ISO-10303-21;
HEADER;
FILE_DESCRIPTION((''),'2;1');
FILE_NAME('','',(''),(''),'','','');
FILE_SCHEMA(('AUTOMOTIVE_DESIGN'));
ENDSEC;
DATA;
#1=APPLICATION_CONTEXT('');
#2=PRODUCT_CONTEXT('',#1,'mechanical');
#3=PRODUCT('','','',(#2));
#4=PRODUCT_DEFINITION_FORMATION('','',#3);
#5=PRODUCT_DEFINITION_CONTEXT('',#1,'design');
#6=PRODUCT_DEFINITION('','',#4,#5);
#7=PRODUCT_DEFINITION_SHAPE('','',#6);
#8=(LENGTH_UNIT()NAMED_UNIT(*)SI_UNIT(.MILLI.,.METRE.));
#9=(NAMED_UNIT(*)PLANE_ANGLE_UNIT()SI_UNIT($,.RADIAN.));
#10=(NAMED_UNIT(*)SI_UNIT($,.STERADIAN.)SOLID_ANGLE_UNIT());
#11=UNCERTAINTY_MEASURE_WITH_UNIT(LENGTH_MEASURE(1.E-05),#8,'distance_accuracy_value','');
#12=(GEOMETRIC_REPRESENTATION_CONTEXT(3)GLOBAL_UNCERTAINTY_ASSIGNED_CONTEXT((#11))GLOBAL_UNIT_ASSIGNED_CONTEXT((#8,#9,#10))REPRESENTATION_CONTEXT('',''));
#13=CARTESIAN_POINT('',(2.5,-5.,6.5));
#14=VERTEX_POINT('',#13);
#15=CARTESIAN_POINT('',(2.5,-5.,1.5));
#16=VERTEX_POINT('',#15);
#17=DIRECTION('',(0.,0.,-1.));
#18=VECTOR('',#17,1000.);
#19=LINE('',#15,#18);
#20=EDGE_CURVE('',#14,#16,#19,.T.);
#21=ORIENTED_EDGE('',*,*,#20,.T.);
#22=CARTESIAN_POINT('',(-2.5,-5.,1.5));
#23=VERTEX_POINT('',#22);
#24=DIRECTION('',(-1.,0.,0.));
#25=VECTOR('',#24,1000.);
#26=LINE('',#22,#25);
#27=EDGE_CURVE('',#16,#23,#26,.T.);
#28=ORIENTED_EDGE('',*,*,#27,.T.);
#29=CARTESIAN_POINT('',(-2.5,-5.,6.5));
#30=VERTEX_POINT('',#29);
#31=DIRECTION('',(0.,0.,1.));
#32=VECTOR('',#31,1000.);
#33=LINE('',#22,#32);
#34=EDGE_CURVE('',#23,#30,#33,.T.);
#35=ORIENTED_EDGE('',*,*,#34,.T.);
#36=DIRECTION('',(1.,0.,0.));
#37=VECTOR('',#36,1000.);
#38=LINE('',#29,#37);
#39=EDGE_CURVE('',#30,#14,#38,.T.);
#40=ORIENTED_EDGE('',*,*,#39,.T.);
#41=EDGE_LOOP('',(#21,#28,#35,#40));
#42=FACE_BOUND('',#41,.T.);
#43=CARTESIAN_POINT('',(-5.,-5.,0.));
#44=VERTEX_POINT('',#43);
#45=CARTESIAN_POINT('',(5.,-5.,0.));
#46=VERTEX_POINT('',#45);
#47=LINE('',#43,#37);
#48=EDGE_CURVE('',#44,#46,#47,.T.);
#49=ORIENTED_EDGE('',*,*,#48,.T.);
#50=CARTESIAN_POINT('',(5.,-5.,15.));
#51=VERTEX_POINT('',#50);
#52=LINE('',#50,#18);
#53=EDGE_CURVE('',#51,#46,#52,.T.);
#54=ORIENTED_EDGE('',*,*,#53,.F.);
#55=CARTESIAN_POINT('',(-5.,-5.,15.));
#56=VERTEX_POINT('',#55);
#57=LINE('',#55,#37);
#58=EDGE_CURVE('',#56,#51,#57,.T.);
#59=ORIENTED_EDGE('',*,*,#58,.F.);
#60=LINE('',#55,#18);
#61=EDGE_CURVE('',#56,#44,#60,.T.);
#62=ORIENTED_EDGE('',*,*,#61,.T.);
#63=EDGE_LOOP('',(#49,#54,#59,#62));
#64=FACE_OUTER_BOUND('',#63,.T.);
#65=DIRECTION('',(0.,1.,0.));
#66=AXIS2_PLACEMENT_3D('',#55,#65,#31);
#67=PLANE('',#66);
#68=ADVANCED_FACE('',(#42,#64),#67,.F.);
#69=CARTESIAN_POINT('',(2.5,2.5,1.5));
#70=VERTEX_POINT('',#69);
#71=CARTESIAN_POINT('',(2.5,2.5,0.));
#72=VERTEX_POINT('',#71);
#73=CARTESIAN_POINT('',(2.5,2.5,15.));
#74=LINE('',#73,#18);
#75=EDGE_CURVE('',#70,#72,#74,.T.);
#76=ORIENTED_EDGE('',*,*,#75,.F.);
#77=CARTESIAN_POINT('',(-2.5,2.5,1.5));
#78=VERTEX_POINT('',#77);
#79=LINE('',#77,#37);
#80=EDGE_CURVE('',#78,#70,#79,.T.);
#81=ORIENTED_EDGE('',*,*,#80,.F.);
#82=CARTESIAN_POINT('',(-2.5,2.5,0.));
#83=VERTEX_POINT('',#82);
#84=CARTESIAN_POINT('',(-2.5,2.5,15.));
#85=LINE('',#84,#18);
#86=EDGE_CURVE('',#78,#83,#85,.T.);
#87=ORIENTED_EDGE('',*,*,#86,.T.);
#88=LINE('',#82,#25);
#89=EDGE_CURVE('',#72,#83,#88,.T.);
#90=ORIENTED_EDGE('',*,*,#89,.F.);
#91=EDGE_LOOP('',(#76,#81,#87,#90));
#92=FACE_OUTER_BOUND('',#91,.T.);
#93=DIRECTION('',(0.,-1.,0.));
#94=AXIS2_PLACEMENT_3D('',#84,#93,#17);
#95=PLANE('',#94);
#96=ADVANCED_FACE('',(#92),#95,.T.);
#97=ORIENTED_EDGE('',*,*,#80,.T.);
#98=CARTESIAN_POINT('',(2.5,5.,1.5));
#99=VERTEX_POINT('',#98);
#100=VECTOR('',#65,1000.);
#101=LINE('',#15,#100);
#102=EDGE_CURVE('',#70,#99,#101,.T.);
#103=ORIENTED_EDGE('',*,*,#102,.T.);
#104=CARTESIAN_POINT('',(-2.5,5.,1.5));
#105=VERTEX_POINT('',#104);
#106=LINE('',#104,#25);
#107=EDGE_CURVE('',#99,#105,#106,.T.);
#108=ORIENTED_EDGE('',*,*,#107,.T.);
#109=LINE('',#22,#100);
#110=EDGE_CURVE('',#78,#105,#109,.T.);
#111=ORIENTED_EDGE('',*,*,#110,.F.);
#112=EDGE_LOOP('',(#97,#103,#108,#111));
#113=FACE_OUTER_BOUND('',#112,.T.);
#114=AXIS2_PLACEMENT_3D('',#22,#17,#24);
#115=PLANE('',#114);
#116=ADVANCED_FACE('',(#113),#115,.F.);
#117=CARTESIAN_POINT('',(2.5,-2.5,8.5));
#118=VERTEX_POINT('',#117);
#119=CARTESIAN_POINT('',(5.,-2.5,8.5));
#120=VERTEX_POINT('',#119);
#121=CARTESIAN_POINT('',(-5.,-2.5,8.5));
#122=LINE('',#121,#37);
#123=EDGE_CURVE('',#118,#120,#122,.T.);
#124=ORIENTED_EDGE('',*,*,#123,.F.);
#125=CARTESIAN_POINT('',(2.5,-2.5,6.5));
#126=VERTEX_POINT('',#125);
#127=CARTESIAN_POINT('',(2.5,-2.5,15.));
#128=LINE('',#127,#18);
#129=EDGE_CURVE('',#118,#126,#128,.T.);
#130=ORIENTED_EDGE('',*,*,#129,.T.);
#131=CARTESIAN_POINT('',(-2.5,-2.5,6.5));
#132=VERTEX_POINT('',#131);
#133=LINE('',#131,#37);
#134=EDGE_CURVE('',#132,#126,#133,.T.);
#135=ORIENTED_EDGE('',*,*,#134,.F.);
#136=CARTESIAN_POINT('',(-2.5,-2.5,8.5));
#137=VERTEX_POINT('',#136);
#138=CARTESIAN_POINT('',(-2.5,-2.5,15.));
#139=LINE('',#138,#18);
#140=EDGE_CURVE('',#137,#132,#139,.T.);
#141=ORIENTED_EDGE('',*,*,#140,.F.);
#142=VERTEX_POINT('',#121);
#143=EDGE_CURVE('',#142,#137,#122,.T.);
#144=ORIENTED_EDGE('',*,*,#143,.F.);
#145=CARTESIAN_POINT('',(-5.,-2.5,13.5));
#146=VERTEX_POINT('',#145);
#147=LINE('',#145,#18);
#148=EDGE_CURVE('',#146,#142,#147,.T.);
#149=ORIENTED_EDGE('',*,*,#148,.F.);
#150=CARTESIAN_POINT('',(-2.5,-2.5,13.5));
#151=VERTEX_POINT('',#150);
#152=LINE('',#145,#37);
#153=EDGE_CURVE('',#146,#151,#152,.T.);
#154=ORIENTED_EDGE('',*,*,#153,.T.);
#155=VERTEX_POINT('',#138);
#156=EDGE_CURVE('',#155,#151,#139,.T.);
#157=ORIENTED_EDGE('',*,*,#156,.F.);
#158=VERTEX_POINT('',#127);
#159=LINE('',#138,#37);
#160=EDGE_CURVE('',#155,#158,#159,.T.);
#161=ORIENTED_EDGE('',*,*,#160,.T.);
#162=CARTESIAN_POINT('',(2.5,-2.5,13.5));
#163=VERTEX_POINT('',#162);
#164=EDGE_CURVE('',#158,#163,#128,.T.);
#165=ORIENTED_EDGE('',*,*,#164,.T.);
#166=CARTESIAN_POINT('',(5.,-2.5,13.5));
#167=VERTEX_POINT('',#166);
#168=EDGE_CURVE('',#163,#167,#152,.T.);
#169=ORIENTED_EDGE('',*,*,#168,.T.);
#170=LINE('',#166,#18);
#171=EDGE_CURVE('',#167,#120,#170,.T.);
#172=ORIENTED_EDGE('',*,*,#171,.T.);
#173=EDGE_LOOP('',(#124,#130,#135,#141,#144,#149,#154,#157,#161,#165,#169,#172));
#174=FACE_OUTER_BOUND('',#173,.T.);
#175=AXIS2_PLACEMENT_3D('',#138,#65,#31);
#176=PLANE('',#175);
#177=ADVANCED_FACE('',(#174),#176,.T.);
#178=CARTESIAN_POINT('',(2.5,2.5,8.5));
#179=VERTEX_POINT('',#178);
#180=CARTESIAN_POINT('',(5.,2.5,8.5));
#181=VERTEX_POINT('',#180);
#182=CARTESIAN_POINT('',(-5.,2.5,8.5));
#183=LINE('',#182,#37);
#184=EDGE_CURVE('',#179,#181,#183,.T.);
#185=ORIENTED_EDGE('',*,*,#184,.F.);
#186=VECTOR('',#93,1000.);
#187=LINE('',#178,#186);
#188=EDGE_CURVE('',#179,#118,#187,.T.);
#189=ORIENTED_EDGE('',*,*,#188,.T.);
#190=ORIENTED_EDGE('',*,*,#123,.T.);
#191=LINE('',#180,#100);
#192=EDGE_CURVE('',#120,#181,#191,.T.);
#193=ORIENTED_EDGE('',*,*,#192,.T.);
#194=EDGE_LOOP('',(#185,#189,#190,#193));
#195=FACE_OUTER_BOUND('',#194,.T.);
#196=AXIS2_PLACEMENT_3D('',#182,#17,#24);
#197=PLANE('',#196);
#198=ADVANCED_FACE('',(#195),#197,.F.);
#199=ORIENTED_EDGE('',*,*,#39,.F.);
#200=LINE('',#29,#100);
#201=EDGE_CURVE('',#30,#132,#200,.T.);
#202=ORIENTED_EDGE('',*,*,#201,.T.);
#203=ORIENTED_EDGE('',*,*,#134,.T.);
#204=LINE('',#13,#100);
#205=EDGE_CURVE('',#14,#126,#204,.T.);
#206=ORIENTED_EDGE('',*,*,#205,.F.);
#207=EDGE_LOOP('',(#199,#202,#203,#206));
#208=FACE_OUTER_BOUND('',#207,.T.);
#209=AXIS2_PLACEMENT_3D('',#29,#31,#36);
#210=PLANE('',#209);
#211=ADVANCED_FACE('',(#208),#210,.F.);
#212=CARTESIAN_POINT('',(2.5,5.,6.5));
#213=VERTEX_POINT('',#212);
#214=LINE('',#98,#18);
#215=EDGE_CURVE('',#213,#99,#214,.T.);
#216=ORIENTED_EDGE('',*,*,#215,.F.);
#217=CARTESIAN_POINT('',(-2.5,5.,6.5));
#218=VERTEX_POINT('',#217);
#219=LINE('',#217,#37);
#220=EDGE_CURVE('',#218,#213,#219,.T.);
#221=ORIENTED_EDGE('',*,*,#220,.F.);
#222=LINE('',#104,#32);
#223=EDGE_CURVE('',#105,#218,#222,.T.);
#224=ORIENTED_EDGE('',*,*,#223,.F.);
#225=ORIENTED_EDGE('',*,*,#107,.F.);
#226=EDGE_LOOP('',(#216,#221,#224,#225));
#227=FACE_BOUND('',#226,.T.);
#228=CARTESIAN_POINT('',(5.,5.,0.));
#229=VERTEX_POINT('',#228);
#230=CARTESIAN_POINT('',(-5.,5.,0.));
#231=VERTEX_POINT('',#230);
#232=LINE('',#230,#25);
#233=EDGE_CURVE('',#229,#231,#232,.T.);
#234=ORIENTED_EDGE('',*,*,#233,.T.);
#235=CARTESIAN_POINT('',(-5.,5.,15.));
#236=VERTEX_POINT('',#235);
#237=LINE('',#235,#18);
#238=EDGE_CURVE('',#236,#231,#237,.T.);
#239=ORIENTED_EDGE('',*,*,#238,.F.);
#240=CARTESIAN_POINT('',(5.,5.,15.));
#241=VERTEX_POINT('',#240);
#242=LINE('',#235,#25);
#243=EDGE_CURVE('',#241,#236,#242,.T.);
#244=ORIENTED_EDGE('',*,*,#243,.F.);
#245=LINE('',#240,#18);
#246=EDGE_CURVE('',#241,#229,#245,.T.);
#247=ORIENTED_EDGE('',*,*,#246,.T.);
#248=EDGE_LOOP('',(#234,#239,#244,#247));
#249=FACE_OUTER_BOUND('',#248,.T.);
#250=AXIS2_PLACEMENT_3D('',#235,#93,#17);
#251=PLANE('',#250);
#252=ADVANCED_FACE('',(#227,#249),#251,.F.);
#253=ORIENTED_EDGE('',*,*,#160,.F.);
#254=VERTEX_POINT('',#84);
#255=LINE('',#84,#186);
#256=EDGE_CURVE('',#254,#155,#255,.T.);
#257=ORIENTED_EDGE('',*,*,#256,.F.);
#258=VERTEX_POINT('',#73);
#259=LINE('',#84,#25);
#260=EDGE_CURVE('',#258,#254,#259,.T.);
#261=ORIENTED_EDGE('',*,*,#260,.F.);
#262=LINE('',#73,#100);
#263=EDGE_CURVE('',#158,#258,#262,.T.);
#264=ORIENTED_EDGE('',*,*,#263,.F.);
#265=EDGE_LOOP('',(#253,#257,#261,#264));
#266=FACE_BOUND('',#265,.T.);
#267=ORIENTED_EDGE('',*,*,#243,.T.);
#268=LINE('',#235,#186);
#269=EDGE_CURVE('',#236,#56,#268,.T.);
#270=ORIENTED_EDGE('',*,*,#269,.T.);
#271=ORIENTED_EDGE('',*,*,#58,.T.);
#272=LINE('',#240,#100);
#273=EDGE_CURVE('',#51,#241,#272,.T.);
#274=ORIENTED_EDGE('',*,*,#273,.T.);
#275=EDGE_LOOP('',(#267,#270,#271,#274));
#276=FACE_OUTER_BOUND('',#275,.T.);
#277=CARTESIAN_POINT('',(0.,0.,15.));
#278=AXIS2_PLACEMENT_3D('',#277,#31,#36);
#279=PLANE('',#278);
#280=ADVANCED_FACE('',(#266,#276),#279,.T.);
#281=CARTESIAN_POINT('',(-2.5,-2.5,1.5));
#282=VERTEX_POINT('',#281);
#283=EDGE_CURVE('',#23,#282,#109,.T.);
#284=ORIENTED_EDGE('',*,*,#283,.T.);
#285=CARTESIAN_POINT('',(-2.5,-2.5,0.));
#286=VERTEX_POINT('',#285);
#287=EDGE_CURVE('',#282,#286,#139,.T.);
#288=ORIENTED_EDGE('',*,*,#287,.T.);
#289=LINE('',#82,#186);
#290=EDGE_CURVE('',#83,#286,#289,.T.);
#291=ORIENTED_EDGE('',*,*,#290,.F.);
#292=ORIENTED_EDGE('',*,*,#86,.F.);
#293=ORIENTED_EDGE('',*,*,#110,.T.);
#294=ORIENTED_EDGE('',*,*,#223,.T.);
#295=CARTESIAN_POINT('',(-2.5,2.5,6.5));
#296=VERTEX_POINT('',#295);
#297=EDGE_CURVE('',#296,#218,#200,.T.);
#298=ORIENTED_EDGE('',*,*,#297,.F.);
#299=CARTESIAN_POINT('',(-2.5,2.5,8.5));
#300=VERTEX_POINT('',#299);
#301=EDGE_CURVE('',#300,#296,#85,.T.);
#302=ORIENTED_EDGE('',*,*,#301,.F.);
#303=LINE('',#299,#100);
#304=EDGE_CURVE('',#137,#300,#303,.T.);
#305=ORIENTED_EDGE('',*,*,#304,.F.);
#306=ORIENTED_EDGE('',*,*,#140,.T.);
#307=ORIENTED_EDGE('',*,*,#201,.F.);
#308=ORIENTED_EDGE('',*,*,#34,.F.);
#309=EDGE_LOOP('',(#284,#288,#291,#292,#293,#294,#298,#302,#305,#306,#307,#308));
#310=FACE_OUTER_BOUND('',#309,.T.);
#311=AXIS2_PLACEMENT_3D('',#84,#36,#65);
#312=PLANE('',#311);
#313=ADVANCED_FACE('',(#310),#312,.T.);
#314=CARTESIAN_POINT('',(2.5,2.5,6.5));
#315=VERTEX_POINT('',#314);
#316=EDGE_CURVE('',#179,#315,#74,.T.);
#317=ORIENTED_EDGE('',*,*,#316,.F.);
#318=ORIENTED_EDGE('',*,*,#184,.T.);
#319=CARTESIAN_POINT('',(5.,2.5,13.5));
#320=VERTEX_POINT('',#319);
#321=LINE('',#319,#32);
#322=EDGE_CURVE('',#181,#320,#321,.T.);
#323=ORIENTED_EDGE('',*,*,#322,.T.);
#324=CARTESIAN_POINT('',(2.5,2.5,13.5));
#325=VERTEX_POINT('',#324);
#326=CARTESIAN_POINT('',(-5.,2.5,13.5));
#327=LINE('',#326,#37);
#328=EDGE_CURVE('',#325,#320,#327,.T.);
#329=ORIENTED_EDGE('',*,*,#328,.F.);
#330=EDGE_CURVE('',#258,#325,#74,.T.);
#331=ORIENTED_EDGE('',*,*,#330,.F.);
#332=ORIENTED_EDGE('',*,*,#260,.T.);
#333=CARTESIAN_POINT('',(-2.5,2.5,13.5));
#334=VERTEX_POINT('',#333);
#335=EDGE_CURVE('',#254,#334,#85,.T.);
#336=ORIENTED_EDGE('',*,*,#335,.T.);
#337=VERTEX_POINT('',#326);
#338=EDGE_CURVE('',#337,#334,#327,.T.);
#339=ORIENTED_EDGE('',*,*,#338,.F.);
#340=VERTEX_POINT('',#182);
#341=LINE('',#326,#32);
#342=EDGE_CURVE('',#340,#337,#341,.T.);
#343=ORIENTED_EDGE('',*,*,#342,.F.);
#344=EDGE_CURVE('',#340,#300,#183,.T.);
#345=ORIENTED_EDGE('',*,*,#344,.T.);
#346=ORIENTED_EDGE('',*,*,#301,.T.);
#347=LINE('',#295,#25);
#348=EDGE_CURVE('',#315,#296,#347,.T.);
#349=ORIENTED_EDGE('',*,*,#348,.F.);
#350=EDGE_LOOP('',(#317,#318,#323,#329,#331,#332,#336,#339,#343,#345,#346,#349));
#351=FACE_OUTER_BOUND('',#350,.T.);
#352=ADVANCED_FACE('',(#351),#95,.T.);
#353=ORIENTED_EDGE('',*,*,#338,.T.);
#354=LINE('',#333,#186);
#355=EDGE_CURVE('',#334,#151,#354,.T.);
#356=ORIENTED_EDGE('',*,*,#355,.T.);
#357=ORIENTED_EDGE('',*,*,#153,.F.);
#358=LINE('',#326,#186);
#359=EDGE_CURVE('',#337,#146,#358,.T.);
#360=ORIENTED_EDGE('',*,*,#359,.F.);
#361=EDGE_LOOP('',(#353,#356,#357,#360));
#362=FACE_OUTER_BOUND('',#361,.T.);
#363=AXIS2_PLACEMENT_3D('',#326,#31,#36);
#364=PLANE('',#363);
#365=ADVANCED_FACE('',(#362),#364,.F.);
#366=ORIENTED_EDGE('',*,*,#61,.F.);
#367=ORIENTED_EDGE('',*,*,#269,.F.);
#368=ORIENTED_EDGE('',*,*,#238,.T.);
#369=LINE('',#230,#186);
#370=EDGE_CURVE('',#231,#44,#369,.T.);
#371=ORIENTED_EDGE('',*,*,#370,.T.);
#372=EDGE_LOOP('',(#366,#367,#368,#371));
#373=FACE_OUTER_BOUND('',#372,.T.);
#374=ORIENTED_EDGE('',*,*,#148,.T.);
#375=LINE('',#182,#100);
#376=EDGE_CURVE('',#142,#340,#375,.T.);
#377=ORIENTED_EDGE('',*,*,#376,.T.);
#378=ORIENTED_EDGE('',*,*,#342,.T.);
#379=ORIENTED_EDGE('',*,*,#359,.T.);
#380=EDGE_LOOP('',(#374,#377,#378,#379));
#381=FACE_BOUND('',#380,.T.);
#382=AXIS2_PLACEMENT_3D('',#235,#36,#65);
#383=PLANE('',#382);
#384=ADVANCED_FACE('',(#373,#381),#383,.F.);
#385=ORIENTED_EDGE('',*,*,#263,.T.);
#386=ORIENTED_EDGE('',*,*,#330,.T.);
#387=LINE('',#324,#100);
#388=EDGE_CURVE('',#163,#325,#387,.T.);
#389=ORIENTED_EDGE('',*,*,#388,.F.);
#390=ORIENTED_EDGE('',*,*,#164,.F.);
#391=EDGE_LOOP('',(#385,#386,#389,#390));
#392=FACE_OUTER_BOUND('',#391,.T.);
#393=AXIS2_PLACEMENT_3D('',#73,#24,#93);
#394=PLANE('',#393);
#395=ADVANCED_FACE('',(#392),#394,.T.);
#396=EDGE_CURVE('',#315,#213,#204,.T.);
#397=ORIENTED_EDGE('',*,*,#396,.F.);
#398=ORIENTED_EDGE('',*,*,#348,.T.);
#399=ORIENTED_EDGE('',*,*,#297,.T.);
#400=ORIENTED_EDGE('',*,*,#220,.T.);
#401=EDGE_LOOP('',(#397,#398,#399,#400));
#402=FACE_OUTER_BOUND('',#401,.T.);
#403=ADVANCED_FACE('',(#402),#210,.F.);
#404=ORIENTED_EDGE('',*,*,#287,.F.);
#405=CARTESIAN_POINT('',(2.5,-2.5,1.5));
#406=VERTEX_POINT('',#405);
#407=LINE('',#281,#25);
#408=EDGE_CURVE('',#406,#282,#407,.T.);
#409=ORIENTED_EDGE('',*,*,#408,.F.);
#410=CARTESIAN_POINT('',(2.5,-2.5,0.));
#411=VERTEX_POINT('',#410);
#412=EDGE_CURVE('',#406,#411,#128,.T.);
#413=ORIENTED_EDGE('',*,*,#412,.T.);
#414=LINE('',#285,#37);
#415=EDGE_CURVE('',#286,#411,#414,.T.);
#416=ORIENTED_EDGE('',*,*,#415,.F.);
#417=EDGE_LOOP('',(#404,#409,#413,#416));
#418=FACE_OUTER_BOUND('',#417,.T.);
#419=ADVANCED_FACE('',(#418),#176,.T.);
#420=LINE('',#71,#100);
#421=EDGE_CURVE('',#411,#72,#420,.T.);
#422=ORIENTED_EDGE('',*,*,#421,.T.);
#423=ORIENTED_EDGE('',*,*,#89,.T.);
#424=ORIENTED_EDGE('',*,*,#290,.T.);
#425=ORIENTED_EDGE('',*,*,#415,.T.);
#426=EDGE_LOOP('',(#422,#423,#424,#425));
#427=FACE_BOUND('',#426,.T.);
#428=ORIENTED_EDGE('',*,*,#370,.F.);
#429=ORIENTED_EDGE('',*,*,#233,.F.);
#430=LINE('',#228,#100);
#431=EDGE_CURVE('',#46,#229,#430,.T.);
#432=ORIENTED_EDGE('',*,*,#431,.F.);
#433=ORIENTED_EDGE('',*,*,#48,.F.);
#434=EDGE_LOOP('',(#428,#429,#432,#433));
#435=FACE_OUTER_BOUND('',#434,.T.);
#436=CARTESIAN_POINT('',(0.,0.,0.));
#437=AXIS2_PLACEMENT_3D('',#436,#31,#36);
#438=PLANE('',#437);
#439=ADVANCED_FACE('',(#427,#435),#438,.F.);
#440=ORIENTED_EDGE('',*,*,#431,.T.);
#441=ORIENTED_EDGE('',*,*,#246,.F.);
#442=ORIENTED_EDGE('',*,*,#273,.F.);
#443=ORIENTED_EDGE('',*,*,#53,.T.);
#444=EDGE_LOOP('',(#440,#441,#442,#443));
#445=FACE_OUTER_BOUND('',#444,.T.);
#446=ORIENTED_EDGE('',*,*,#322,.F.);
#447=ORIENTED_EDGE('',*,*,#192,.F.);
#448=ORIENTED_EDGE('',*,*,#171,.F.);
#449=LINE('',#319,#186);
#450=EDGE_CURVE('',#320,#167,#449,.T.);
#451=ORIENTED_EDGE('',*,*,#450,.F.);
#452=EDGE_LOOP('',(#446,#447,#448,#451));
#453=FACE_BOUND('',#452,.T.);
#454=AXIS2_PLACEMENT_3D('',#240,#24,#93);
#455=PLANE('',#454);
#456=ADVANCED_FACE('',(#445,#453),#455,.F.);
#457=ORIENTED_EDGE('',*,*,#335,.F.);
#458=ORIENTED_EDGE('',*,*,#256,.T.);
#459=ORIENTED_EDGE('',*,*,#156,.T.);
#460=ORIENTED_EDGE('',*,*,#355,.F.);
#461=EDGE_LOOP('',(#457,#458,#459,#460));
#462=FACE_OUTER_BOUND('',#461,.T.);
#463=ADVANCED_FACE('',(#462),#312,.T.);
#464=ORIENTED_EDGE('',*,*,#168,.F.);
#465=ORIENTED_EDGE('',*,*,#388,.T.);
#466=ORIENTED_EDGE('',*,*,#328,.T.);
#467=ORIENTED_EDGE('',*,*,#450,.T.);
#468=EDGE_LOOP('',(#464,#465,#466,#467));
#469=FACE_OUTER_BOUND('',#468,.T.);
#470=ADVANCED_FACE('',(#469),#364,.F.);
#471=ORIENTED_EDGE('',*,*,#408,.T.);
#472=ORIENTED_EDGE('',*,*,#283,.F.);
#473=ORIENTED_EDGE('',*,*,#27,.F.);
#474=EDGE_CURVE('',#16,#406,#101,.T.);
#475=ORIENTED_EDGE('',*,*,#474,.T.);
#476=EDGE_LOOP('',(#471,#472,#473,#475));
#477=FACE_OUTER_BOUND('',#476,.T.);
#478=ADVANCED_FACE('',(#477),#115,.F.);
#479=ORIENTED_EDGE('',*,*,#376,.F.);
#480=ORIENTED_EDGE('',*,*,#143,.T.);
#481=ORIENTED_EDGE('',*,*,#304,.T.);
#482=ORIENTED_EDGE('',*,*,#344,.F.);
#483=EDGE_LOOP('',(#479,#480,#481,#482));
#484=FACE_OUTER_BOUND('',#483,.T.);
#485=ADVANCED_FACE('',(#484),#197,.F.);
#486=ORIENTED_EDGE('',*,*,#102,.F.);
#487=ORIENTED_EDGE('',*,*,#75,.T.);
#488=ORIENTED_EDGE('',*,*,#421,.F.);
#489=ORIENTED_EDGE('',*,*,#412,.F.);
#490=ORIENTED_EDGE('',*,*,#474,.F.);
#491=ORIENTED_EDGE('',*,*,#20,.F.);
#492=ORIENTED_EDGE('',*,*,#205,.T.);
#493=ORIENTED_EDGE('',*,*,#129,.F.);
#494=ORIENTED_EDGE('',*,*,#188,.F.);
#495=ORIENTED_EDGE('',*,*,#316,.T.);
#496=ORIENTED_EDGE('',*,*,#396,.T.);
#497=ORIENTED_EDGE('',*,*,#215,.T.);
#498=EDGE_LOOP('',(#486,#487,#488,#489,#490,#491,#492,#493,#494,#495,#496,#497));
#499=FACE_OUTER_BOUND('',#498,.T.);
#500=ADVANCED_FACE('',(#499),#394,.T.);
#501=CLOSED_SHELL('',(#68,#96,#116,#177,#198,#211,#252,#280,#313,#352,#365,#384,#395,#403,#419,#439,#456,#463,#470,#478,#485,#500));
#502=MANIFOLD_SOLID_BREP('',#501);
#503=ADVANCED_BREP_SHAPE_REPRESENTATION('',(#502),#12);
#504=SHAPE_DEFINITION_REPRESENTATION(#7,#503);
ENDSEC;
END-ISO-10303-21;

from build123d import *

# Parameters (mm, degrees)
SKETCH1_W           = 10
SKETCH1_H           = 10
SKETCH1_W_2         = 5
SKETCH1_H_2         = 5
BOSS_EXTRUDE1_DEPTH = 15
SKETCH2_W           = 5
SKETCH2_H           = 5
CUT_EXTRUDE1_DEPTH  = 19.708286934
SKETCH3_W           = 5
SKETCH3_H           = 5
CUT_EXTRUDE2_DEPTH  = 19.708286934


with BuildPart() as part:
    # Sketch1 → Boss-Extrude1 (new body)
    with BuildSketch(Plane.XY):
        Rectangle(SKETCH1_W, SKETCH1_H)
        Rectangle(SKETCH1_W_2, SKETCH1_H_2, mode=Mode.SUBTRACT)
    extrude(amount=BOSS_EXTRUDE1_DEPTH)

    # Sketch2 → Cut-Extrude1 (cut, through all)
    with BuildSketch(Plane(origin=(0, 5, 0), x_dir=(1, 0, 0), z_dir=(0, 1, 0))):
        with Locations((0, -4)):
            Rectangle(SKETCH2_W, SKETCH2_H)
    extrude(amount=-CUT_EXTRUDE1_DEPTH, mode=Mode.SUBTRACT)

    # Sketch3 → Cut-Extrude2 (cut, through all)
    with BuildSketch(Plane(origin=(5, 0, 0), x_dir=(0, 0, -1), z_dir=(1, 0, 0))):
        with Locations((-11, 0)):
            Rectangle(SKETCH3_W, SKETCH3_H)
    extrude(amount=-CUT_EXTRUDE2_DEPTH, mode=Mode.SUBTRACT)


solid = part.part
